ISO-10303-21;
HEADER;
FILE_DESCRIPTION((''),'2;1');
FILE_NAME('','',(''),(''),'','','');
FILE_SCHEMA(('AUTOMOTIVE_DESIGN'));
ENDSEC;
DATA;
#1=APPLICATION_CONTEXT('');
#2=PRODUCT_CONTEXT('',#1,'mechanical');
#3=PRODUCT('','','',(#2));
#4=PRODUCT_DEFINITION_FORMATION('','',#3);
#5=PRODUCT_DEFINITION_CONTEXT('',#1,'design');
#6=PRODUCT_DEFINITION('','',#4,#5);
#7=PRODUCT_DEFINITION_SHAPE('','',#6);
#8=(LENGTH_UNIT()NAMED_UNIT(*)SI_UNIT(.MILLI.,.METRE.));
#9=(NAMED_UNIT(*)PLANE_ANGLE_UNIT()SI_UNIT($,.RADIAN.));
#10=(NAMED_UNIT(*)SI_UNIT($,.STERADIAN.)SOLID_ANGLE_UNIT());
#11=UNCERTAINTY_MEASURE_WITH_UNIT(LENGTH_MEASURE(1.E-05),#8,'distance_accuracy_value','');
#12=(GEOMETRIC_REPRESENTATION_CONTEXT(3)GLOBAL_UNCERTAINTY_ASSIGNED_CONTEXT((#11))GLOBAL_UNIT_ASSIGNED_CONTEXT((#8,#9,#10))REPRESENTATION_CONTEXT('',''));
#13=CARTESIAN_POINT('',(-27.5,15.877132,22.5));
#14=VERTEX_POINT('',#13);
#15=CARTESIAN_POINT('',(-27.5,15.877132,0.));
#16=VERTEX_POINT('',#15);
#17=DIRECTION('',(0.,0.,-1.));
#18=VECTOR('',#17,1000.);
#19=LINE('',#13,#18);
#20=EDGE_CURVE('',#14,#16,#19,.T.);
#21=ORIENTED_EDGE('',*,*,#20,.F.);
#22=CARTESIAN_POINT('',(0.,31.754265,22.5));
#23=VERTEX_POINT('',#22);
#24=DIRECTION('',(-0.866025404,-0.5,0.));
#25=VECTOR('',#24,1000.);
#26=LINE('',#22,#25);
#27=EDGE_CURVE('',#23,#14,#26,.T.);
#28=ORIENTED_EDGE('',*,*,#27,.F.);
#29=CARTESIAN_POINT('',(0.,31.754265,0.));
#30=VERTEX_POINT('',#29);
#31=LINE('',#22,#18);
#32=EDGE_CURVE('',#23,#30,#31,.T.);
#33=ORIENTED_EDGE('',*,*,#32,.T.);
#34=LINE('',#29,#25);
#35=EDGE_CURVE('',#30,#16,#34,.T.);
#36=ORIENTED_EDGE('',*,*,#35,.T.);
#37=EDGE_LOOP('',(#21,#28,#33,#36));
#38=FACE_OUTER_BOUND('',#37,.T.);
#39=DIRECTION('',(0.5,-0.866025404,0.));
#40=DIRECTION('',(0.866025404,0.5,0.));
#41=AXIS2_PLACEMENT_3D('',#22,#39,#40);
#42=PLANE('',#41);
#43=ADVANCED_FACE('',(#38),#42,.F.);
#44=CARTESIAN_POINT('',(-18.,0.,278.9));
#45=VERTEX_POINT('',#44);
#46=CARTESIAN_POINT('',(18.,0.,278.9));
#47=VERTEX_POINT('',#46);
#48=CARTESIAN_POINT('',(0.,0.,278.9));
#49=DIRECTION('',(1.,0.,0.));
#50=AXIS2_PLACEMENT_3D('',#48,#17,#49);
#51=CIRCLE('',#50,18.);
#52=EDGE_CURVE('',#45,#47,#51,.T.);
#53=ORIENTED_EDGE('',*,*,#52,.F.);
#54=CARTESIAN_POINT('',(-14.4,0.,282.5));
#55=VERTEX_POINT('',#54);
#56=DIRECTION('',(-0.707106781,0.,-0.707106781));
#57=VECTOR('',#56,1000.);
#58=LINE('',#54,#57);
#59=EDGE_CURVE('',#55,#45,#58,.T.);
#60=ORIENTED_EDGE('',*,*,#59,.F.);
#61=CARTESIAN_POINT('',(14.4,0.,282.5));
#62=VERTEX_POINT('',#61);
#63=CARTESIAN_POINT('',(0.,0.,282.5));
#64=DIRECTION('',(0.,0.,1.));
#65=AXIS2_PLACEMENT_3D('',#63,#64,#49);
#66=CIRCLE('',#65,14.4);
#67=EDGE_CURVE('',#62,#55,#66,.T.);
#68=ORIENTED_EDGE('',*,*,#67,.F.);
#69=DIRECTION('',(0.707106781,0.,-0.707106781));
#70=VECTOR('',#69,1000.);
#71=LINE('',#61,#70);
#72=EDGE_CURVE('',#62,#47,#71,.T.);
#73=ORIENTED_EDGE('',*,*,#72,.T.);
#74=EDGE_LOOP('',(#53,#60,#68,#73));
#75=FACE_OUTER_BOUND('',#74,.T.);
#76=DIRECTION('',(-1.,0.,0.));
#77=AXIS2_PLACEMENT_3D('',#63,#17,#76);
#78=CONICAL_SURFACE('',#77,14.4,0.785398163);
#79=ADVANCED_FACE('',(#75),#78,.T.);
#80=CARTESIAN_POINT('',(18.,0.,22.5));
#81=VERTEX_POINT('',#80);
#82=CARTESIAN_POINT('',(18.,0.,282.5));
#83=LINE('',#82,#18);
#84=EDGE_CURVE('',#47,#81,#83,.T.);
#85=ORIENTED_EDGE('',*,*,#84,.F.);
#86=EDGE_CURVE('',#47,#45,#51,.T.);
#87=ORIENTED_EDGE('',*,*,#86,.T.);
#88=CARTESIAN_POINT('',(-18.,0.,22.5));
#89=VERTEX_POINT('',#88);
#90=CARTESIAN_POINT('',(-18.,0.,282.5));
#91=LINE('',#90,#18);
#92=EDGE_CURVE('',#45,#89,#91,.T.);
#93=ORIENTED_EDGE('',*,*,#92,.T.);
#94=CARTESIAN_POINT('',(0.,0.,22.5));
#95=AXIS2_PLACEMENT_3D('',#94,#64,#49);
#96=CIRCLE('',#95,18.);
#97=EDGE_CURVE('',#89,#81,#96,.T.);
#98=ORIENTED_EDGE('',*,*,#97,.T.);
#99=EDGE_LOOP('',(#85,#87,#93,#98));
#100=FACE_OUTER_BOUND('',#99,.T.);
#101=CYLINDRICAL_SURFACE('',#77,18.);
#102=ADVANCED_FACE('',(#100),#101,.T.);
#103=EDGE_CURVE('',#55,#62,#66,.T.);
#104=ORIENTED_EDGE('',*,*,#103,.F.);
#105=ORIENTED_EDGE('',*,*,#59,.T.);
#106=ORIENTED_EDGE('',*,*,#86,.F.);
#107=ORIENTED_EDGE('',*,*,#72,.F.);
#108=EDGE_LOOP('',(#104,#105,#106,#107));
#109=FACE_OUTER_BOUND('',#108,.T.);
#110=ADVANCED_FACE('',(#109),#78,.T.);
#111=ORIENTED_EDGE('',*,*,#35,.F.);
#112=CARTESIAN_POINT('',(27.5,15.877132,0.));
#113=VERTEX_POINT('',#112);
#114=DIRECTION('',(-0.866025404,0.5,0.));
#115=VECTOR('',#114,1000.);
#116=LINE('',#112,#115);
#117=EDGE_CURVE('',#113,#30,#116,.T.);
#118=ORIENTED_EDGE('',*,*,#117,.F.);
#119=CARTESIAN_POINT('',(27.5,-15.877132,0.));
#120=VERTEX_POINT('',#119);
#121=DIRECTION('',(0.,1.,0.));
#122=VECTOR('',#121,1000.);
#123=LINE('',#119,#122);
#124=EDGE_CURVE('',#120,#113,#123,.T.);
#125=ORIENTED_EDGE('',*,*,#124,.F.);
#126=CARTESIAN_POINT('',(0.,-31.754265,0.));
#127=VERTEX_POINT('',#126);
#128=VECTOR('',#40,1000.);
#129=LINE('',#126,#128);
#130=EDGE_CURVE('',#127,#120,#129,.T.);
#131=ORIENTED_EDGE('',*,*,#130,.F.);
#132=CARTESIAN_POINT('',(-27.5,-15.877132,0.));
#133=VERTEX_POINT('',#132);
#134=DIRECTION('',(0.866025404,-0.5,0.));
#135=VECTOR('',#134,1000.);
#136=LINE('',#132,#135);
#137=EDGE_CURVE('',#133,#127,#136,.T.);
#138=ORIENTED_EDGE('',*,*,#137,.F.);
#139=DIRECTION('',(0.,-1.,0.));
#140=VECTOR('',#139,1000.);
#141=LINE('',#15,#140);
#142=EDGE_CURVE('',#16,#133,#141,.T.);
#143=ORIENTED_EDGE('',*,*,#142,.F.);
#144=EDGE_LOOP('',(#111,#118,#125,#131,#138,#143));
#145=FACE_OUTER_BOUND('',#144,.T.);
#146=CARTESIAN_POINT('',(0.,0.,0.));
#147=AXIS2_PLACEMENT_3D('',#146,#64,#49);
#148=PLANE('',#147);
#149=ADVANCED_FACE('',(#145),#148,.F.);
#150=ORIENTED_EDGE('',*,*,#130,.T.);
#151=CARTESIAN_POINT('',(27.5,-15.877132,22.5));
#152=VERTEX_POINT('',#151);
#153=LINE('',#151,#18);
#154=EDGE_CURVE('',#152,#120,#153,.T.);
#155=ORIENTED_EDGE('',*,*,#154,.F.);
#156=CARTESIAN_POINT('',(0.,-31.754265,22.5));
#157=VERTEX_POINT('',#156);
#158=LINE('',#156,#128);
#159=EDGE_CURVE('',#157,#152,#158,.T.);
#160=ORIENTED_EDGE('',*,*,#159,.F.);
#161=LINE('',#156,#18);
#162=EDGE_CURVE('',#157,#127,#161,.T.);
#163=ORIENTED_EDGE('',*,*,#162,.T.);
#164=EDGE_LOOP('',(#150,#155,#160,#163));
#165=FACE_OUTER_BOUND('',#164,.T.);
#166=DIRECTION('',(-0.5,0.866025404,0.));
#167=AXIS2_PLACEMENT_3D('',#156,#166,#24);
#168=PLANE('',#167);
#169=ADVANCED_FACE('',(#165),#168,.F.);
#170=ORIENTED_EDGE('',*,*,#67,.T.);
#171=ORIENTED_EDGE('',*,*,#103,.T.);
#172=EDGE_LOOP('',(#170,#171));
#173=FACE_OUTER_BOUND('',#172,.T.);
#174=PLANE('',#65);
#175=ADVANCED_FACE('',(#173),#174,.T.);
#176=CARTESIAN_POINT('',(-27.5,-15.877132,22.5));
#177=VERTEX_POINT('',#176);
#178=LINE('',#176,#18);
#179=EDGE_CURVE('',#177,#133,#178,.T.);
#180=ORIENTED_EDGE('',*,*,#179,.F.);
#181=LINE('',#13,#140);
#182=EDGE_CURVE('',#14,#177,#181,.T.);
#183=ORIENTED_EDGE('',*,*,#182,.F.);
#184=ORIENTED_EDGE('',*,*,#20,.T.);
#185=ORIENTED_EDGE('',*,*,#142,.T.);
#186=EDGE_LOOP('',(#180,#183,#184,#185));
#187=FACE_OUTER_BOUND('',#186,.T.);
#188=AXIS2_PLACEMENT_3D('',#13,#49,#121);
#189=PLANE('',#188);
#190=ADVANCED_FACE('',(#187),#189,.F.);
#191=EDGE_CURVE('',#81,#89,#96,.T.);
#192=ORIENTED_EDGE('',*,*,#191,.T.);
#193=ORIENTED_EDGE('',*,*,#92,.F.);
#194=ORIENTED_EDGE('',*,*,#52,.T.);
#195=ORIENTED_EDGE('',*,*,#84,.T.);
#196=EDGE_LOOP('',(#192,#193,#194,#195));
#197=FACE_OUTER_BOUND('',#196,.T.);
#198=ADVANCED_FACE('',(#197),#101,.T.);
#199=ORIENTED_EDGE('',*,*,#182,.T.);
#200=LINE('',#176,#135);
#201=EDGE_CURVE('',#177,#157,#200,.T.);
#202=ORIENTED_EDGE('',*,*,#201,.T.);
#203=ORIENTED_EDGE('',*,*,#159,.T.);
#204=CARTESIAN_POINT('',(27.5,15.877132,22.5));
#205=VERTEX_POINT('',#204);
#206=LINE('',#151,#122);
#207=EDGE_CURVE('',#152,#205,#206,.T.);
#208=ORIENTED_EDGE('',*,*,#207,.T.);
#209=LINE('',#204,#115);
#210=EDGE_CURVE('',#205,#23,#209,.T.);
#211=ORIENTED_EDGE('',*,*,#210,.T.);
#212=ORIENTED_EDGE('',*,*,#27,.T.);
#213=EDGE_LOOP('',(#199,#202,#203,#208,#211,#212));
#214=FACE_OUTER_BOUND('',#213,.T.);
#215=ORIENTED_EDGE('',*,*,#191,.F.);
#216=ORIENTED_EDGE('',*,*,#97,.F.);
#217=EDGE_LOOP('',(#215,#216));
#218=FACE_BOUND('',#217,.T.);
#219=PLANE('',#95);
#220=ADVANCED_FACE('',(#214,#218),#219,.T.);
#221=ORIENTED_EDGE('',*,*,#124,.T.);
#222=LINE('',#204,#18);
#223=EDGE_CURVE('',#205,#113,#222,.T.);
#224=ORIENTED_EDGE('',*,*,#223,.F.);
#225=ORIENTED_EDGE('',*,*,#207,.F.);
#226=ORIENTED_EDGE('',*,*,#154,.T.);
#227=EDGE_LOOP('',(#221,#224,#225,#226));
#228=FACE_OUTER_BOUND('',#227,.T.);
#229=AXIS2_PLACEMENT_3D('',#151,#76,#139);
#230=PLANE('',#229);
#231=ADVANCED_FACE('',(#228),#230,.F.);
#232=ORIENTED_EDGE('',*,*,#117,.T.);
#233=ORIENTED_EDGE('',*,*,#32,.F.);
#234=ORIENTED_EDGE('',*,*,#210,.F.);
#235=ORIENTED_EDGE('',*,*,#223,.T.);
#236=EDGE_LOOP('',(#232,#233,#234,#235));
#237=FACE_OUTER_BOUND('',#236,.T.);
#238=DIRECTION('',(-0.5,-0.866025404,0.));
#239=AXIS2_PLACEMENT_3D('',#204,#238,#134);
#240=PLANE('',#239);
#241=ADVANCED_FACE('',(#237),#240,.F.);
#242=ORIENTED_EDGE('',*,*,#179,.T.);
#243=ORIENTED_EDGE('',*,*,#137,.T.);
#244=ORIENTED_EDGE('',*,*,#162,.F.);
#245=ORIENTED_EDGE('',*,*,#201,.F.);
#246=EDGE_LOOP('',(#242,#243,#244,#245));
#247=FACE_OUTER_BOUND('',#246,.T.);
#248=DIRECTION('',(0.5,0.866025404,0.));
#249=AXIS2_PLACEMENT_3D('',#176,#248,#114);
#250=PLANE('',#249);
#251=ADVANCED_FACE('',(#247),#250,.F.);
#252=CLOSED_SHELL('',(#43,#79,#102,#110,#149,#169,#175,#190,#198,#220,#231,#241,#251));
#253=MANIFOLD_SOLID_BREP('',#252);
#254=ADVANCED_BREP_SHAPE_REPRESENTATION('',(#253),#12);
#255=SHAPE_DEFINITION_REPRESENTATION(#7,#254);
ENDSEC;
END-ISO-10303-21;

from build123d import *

# Parameters (mm, degrees)
BOSS_EXTRUDE1_DEPTH = 22.5
SKETCH3_R           = 18
BOSS_EXTRUDE2_DEPTH = 260
CHAMFER1_SIZE       = 3.6


with BuildPart() as part:
    # Sketch1 → Boss-Extrude1 (new body)
    with BuildSketch(Plane.XY):
        Polygon((27.5, 15.877132403), (0, 31.754264805), (-27.5, 15.877132403), (-27.5, -15.877132403), (0, -31.754264805), (27.5, -15.877132403), align=None)
    extrude(amount=BOSS_EXTRUDE1_DEPTH)

    # Sketch3 → Boss-Extrude2 (add)
    with BuildSketch(Plane.XY.offset(22.5)):
        Circle(SKETCH3_R)
    extrude(amount=BOSS_EXTRUDE2_DEPTH)

    # Chamfer1
    chamfer1_edges = [part.edges().sort_by_distance(p)[0] for p in [
        (-18, 0, 282.5),
    ]]
    chamfer(chamfer1_edges, length=CHAMFER1_SIZE)


solid = part.part
